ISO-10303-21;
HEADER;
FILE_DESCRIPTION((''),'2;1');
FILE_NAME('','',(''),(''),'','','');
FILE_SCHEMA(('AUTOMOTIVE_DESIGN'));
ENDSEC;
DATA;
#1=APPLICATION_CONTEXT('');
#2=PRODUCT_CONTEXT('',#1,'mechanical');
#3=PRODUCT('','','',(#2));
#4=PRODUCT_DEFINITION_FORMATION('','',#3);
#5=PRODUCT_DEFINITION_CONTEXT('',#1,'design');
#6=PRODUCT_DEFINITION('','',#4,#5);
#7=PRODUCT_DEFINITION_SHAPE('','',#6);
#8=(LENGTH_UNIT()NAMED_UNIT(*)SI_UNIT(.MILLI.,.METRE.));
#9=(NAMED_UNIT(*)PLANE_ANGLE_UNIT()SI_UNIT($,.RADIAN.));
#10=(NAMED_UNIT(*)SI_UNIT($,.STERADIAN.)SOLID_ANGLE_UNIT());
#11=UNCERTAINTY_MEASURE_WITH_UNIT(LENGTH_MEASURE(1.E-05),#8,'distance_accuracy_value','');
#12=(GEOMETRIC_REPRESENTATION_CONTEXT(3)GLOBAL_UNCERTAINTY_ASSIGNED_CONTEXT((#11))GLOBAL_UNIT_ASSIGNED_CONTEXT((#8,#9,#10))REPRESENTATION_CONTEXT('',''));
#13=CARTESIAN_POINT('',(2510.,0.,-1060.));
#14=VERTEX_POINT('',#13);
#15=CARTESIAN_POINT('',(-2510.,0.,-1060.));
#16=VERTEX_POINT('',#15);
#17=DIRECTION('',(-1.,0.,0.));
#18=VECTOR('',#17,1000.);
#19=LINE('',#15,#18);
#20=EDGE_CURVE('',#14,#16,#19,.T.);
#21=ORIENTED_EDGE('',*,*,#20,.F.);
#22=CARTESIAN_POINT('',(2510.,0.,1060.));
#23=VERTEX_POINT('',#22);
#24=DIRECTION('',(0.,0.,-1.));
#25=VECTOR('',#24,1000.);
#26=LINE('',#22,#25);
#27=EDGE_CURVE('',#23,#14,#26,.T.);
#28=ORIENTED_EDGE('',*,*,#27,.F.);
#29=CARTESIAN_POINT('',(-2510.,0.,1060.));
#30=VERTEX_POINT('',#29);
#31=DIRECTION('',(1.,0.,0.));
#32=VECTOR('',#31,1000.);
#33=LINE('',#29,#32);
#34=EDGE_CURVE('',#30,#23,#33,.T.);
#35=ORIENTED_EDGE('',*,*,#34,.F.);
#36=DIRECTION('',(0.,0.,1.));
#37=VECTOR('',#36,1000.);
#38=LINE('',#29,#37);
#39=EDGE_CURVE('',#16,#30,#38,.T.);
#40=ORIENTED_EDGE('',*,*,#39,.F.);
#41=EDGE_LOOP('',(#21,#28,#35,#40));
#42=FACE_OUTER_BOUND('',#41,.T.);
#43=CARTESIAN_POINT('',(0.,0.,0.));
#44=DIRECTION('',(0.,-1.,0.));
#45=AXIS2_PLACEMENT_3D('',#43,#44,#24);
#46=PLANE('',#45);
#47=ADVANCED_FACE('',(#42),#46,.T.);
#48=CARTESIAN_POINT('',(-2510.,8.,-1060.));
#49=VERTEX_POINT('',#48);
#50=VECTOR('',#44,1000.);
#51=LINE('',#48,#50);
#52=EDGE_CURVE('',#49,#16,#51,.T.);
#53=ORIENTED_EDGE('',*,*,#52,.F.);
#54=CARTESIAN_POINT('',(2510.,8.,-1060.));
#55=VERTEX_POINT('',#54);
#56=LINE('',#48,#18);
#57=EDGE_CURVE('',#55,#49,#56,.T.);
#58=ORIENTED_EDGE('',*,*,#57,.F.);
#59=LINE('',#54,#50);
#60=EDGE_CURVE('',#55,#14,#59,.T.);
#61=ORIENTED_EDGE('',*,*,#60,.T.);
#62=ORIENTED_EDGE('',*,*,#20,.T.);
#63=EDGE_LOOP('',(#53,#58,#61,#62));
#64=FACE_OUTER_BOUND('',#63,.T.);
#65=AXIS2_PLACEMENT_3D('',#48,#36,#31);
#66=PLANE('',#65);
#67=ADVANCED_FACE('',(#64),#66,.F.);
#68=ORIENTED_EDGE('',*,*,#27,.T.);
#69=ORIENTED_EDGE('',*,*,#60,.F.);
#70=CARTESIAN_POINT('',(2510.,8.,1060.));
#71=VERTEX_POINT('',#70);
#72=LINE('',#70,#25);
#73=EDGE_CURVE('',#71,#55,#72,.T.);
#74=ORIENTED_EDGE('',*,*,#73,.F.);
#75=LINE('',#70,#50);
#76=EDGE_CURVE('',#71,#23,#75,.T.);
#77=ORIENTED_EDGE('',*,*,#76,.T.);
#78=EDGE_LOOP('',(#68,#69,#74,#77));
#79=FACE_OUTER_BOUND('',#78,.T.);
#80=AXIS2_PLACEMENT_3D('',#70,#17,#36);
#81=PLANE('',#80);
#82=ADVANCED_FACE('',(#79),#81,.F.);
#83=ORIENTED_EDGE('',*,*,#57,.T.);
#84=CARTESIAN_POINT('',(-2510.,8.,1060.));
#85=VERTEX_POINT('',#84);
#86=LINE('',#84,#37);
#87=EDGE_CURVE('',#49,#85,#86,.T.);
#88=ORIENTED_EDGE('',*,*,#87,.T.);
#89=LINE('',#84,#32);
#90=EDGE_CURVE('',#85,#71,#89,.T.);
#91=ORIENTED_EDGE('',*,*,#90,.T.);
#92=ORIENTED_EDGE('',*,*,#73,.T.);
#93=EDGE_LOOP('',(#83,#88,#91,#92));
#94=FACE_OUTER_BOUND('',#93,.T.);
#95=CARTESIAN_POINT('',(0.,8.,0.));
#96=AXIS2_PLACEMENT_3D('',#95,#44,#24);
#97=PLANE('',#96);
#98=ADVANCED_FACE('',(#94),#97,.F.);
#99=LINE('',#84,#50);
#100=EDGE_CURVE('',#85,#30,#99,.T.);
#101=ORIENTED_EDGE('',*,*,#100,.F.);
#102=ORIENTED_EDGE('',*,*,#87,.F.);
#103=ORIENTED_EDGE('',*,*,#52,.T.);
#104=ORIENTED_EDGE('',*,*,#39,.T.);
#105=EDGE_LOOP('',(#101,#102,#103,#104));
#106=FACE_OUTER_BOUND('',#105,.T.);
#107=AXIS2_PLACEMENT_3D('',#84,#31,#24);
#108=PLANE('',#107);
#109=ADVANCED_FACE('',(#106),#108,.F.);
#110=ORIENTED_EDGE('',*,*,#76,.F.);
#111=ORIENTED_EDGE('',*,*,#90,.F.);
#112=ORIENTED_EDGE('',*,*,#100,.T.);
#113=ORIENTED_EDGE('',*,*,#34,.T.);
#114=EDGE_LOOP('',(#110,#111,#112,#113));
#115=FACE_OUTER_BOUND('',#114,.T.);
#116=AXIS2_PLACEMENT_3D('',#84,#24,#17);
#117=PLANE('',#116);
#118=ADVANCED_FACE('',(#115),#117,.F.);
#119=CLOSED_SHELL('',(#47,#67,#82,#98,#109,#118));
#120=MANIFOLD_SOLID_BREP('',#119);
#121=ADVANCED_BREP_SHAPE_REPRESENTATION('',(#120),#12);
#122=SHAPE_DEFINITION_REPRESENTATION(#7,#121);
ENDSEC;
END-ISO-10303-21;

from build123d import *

# Parameters (mm, degrees)
SKETCH_1_W           = 5020
SKETCH_1_H           = 2120
BOSS_EXTRUDE_1_DEPTH = 8


with BuildPart() as part:
    # Sketch 1 → Boss-Extrude 1 (new body)
    with BuildSketch(Plane(origin=(0, 0, 0), x_dir=(1, 0, 0), z_dir=(0, 1, 0))):
        Rectangle(SKETCH_1_W, SKETCH_1_H)
    extrude(amount=BOSS_EXTRUDE_1_DEPTH)


solid = part.part
